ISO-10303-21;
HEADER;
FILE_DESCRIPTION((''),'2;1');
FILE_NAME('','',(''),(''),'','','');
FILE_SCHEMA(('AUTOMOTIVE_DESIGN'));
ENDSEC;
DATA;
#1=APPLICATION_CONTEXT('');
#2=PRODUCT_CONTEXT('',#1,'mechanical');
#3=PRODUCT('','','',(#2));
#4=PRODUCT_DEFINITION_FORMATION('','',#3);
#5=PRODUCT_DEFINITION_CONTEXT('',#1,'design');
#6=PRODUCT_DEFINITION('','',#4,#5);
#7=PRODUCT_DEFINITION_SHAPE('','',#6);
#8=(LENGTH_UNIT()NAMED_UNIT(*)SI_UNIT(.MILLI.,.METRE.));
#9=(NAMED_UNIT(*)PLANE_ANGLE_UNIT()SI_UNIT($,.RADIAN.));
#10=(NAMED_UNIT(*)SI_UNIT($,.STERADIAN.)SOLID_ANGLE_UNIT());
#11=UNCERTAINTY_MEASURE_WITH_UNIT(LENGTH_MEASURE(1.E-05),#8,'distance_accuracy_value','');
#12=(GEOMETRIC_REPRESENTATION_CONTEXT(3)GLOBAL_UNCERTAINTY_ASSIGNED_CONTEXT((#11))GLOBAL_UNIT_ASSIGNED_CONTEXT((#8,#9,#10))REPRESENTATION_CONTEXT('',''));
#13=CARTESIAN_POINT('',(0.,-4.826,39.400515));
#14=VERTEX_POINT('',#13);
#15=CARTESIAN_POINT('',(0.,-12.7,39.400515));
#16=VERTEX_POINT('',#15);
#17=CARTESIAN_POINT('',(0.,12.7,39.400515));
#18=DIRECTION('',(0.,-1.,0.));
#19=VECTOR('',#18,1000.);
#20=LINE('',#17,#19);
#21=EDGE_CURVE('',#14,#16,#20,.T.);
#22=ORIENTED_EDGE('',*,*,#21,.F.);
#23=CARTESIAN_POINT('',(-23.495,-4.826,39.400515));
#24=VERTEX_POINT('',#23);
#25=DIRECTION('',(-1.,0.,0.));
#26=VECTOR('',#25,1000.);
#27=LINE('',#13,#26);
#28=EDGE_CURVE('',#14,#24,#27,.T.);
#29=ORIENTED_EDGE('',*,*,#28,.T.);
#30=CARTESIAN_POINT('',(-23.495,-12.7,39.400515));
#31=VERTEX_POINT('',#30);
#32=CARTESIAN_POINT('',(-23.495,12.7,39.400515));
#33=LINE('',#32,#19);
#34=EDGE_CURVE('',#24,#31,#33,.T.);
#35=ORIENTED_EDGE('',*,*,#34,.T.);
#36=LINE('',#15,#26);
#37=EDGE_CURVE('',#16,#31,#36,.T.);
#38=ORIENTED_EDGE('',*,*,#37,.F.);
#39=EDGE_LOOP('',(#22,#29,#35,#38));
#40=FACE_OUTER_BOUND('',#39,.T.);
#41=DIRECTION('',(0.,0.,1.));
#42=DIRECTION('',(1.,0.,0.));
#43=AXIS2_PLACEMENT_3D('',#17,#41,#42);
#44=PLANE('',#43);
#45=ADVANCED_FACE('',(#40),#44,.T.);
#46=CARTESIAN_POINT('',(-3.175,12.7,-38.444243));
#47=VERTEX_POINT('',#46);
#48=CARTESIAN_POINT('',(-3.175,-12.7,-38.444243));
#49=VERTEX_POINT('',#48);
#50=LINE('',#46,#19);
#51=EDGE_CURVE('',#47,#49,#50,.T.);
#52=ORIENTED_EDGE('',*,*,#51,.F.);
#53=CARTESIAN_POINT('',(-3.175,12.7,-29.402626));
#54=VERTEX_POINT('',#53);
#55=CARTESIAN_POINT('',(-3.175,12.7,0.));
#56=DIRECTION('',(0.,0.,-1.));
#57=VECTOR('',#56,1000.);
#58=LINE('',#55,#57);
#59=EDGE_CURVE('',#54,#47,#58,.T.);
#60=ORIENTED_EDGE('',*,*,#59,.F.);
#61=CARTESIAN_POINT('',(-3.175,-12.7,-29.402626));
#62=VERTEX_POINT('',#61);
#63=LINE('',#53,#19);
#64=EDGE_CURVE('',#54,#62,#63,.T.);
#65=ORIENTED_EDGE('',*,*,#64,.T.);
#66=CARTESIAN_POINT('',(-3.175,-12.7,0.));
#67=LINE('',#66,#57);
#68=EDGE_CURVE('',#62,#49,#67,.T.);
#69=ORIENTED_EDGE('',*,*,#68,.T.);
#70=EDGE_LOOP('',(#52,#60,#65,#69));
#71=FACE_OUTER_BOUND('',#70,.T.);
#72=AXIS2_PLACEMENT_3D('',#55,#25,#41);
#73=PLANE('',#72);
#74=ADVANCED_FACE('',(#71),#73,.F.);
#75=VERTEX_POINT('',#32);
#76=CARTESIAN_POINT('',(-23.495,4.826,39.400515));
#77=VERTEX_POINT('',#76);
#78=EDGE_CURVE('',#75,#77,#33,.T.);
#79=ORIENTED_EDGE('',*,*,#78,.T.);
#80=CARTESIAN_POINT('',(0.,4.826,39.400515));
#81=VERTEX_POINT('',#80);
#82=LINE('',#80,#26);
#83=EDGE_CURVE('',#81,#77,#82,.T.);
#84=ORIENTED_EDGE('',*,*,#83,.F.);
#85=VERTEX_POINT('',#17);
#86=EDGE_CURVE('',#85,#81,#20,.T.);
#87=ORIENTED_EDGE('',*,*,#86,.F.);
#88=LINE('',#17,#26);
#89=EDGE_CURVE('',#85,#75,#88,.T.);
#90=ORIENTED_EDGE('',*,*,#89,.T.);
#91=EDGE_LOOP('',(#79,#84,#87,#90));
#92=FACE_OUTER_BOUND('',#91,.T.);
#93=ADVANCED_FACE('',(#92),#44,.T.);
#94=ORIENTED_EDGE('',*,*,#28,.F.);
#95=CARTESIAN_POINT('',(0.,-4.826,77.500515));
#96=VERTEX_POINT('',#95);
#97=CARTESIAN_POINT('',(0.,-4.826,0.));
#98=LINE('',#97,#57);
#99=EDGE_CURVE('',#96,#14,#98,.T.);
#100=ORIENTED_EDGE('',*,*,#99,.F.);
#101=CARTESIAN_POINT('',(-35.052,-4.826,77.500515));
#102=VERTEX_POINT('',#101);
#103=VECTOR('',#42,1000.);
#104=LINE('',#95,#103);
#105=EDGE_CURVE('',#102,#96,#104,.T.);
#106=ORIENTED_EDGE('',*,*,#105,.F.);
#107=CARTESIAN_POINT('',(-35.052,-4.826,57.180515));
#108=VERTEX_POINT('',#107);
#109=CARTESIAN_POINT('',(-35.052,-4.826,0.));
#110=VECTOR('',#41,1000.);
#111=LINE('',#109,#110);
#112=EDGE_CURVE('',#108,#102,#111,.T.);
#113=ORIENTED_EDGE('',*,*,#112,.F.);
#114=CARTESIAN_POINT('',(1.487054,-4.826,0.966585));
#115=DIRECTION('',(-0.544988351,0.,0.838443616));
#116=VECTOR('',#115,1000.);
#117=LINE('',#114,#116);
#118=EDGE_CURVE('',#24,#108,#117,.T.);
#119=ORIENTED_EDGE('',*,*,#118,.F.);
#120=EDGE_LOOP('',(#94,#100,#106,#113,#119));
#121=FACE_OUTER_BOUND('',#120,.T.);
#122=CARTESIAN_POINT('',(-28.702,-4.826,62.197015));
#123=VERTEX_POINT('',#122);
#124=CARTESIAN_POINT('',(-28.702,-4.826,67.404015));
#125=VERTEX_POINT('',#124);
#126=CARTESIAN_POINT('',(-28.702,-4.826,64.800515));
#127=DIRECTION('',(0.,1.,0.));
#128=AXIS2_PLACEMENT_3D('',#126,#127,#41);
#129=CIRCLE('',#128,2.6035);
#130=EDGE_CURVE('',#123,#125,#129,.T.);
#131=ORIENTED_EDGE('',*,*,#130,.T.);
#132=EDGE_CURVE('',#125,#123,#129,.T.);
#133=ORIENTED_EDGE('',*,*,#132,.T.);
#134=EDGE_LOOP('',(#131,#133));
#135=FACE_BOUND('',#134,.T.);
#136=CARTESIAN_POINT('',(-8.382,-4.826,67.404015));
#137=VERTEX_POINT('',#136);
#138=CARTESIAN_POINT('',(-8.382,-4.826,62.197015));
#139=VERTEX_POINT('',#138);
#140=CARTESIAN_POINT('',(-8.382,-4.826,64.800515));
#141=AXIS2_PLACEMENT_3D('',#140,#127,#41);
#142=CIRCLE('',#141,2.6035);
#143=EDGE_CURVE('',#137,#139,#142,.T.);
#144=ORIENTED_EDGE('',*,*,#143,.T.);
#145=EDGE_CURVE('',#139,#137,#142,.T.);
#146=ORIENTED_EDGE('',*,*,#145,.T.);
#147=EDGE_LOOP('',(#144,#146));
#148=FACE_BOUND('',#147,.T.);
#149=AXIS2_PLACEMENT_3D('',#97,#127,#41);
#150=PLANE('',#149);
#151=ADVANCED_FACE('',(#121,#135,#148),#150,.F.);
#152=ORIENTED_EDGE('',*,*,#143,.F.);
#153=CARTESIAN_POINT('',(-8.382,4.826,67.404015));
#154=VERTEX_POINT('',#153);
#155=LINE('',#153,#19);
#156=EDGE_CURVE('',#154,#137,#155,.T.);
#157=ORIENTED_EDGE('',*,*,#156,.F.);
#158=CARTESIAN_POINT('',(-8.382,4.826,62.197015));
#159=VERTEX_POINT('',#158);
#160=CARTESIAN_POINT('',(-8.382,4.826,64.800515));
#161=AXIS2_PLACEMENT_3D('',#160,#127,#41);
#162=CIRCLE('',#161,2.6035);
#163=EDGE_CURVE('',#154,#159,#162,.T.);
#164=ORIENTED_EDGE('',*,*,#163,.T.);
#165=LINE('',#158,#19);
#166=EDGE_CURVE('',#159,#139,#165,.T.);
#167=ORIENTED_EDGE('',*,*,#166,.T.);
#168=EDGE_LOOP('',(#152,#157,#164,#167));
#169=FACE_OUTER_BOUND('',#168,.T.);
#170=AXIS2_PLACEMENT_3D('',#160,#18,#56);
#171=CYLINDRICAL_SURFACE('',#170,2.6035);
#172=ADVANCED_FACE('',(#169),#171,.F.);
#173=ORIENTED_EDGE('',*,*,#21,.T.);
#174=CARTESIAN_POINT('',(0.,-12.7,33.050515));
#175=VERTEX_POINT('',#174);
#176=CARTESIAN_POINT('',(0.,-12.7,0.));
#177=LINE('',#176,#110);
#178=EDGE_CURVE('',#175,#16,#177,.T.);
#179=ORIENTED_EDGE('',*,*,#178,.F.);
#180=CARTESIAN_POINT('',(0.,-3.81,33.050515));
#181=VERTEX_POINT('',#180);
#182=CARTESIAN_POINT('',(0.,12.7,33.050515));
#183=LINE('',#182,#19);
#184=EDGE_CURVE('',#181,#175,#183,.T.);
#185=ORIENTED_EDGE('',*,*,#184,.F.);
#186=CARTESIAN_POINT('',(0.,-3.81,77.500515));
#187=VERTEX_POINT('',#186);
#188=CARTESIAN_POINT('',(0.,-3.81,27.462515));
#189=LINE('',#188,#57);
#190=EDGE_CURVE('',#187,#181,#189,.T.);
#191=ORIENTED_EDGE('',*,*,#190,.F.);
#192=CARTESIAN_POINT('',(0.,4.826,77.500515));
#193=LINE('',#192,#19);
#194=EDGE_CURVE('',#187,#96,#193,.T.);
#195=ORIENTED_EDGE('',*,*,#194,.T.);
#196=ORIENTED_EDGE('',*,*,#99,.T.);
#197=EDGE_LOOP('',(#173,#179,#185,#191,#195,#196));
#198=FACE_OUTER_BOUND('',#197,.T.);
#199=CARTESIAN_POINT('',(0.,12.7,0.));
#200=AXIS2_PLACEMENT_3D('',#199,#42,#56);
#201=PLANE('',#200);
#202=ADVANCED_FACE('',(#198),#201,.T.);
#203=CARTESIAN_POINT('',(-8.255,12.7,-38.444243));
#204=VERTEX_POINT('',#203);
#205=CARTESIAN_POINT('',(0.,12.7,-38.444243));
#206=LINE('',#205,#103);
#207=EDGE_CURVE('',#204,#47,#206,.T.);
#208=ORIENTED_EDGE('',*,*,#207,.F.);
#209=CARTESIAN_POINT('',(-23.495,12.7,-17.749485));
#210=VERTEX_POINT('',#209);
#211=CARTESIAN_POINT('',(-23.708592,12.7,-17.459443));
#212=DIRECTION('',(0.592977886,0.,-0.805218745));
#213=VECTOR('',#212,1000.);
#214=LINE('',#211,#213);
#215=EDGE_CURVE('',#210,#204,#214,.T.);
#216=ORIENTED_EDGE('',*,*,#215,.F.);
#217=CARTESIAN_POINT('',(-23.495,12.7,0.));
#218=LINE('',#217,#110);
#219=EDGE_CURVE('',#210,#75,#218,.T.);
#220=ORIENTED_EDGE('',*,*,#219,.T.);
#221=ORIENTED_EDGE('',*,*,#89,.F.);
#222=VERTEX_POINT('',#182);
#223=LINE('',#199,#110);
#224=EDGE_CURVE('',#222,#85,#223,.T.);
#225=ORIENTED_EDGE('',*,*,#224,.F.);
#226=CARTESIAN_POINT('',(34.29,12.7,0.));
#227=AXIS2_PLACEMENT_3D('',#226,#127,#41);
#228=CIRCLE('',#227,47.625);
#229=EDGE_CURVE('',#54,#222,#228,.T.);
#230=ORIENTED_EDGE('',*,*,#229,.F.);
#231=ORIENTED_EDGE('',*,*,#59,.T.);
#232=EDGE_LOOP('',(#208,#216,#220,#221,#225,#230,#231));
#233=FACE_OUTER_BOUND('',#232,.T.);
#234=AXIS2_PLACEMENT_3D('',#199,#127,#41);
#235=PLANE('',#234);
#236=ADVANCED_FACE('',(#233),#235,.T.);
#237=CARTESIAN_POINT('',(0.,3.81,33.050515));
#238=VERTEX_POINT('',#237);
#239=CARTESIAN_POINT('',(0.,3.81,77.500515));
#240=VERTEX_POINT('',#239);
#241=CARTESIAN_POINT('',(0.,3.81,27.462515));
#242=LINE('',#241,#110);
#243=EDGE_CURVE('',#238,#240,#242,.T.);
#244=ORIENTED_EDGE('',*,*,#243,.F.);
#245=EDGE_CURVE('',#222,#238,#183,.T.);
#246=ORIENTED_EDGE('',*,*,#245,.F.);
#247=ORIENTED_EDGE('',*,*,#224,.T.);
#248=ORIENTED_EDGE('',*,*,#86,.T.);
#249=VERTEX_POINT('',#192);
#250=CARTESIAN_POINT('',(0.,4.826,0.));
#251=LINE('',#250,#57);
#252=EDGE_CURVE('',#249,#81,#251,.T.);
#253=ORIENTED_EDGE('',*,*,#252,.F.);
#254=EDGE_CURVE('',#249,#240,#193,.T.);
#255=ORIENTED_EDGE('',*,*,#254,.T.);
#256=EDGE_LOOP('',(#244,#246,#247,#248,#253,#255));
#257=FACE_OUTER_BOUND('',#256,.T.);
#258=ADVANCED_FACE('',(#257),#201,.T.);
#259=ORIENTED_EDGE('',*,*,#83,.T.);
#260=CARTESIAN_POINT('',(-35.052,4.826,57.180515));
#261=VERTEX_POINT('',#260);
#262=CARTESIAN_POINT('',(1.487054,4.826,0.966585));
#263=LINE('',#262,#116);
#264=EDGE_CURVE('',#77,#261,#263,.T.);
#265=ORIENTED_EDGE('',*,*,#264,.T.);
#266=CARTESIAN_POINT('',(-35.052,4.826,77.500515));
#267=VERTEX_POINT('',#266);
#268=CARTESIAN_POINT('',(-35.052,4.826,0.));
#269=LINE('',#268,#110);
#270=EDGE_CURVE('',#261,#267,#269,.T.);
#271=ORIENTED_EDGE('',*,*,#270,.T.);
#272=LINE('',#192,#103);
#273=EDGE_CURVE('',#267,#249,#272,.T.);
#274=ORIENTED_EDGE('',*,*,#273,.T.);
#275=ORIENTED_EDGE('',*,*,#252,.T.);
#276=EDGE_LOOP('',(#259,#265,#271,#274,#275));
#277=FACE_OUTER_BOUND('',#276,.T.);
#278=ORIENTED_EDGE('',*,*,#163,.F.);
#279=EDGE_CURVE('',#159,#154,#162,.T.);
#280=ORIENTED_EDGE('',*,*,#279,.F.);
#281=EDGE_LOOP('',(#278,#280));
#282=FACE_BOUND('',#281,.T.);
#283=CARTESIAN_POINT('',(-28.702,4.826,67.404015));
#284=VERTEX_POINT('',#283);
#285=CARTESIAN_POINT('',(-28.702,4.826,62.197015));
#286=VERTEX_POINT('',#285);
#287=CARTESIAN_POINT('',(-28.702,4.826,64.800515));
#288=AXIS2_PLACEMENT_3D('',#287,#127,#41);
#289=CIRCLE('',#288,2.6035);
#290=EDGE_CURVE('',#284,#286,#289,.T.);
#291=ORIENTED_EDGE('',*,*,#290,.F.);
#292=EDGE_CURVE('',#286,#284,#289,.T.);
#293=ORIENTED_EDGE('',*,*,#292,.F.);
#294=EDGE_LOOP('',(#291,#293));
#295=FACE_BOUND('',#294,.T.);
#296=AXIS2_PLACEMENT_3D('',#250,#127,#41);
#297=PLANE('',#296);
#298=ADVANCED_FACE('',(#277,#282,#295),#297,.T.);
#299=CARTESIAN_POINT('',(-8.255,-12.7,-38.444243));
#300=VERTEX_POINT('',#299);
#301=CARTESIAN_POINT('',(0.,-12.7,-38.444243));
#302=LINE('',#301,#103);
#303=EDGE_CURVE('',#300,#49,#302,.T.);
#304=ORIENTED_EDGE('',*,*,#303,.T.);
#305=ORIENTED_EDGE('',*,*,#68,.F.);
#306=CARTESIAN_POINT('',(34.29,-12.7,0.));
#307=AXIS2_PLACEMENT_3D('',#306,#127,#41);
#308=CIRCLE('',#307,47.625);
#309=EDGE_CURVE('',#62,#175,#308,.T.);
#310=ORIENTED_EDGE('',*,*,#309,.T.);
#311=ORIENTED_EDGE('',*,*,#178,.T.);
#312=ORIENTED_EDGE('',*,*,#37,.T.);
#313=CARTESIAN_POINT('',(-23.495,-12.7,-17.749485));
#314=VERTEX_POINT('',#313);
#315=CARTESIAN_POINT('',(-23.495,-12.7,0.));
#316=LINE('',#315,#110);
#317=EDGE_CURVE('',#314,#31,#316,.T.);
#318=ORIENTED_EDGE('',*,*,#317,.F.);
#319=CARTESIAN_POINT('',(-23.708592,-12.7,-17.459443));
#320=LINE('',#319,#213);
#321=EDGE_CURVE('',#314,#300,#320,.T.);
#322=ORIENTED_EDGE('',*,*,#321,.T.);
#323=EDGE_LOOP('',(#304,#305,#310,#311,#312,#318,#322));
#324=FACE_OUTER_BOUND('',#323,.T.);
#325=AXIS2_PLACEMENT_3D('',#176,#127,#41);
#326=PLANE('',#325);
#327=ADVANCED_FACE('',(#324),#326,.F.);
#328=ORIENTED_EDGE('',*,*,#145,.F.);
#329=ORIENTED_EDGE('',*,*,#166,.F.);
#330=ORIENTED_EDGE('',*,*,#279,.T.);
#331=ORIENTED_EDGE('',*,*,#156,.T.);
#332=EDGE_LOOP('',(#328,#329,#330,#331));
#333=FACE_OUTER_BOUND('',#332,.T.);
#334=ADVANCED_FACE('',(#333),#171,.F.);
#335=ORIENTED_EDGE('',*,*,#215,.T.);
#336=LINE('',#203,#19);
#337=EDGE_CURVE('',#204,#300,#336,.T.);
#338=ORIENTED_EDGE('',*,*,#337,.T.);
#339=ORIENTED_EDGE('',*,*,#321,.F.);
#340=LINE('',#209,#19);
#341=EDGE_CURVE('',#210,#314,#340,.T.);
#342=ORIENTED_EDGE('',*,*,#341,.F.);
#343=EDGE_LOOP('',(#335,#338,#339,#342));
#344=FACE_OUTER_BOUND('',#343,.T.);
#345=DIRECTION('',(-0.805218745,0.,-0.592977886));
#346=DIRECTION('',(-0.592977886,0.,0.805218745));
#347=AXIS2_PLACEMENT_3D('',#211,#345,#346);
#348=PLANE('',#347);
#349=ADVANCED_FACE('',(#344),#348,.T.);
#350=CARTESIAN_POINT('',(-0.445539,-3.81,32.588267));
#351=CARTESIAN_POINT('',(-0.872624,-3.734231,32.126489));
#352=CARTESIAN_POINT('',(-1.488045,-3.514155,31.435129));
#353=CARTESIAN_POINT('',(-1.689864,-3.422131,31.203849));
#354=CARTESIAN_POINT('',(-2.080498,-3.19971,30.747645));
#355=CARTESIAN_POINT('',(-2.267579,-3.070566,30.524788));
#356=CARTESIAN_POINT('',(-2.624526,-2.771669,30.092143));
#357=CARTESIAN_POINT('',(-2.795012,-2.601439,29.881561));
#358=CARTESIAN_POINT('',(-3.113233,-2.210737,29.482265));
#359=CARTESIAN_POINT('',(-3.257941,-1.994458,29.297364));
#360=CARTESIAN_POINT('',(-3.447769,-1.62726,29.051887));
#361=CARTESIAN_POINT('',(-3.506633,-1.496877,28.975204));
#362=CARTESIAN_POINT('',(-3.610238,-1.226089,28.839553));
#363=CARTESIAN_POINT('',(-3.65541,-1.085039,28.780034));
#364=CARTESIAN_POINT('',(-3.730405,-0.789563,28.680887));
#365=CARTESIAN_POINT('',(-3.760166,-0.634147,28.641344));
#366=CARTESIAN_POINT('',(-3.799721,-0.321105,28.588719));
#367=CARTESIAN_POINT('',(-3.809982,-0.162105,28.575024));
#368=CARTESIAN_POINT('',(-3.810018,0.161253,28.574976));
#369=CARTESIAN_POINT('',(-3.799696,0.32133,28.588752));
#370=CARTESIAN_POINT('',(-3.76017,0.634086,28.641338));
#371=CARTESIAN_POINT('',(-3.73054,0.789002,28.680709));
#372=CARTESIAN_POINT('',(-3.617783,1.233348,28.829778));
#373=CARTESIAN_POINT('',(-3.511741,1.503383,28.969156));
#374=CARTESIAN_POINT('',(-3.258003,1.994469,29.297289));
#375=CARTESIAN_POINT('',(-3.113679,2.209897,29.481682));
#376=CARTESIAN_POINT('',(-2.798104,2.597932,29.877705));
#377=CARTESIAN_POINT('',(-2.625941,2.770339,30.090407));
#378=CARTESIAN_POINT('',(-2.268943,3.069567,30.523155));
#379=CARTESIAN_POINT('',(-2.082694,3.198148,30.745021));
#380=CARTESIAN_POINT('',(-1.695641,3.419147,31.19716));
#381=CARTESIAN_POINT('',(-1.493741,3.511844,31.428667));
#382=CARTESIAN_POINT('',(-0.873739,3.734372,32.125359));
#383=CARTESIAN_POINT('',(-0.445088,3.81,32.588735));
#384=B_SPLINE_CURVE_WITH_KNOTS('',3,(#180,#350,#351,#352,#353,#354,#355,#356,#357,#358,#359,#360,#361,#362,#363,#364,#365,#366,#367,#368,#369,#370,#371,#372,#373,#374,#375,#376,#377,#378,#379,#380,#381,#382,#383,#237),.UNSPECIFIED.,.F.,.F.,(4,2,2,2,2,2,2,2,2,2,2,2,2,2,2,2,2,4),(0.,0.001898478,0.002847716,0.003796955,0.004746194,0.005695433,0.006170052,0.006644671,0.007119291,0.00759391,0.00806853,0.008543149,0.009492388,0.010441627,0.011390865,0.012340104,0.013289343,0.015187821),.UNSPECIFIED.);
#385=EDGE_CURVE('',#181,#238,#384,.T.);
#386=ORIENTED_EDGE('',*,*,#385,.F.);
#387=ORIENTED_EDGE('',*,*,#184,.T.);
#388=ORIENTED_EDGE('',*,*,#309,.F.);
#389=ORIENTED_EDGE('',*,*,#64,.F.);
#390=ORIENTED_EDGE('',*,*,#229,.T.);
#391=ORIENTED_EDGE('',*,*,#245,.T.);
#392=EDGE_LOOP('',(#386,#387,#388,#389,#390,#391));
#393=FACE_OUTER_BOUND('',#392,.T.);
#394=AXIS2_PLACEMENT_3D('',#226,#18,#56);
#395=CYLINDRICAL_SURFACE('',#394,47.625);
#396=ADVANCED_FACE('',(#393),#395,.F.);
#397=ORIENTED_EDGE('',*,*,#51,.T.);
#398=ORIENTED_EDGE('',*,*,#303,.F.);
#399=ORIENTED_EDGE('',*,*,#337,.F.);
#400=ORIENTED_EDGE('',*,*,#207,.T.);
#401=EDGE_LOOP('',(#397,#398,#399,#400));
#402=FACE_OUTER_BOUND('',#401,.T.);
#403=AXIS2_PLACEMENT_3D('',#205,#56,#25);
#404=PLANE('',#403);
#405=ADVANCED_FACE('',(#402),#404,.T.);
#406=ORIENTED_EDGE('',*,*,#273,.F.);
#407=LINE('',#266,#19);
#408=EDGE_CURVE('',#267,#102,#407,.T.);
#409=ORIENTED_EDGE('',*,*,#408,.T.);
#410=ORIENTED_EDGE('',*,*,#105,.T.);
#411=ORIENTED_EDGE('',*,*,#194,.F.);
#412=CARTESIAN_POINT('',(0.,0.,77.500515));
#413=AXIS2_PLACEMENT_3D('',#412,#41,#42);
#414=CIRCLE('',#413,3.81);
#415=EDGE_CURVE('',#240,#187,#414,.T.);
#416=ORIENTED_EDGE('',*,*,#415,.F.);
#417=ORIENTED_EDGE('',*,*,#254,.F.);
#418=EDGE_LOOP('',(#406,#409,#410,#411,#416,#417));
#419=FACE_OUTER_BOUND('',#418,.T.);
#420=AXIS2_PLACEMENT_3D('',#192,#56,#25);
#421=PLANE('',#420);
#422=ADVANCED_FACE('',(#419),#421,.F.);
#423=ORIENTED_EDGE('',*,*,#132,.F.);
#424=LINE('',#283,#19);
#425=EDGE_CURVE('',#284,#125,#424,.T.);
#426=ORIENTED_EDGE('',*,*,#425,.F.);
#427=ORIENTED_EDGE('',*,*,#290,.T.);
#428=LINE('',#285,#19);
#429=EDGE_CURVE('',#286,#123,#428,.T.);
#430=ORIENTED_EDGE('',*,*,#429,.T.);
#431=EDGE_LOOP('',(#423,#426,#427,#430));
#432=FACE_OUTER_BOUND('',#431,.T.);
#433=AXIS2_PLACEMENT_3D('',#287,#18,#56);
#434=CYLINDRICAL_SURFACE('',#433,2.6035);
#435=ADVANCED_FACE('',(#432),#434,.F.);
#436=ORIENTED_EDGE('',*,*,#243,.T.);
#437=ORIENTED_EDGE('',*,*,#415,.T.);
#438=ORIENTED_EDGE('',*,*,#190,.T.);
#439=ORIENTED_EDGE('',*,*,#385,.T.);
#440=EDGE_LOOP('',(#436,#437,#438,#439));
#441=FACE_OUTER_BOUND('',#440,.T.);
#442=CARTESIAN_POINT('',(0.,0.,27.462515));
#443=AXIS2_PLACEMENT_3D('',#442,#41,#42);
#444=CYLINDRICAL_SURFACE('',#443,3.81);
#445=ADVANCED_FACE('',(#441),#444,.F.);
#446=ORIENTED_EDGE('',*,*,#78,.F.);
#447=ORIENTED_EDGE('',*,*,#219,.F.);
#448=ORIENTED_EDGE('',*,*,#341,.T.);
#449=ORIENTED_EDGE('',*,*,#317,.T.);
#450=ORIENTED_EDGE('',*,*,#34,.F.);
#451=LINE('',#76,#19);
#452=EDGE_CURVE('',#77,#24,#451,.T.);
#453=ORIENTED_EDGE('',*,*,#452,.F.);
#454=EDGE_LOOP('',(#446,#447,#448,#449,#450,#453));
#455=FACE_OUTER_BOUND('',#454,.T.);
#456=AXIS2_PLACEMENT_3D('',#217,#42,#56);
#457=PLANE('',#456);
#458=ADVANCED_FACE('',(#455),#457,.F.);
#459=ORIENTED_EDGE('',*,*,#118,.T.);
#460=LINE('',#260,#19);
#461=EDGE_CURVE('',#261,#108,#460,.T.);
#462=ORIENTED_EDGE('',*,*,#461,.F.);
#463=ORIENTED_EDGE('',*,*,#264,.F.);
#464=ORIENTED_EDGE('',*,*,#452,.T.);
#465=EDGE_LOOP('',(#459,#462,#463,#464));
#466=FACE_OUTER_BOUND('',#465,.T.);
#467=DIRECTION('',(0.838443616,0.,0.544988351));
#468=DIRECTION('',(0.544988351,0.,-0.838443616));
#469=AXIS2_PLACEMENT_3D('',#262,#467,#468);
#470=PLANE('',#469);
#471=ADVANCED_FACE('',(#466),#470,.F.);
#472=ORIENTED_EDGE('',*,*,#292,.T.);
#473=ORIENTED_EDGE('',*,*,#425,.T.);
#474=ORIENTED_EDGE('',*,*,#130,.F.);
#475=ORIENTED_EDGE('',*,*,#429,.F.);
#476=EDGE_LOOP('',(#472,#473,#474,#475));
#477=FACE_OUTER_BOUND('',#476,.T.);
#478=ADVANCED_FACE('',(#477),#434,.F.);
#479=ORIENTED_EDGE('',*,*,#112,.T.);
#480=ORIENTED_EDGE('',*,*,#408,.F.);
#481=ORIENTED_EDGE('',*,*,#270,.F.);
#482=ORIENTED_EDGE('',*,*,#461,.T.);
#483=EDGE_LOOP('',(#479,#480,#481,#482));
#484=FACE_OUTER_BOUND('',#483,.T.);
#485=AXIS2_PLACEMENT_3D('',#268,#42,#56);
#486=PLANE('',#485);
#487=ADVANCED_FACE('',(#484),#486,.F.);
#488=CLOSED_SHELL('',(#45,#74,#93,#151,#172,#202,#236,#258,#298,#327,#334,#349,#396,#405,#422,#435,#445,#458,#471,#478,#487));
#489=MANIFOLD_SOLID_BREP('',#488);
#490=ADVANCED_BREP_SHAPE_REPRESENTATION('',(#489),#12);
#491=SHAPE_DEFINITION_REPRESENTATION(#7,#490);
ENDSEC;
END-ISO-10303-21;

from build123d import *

# Parameters (mm, degrees)
BOSS_EXTRUDE1_DEPTH = 12.7
SKETCH1_5_R         = 2.6035
BOSS_EXTRUDE2_DEPTH = 4.826
SKETCH2_R           = 3.81
CUT_EXTRUDE1_DEPTH  = 50.038


with BuildPart() as part:
    # Sketch1 → Boss-Extrude1 (new, symmetric)
    with BuildSketch(Plane(origin=(0, 0, 0), x_dir=(1, 0, 0), z_dir=(0, 1, 0))):
        with BuildLine():
            Line((-23.495, 17.749485254), (-23.495, -39.400514746))
            Line((-23.495, -39.400514746), (0, -39.400514746))
            Line((0, -39.400514746), (0, -33.050514746))
            ThreePointArc((0, -33.050514746), (-13.273575299, -2.418042558), (-3.175, 29.402625733))
            Line((-3.175, 29.402625733), (-3.175, 38.444242963))
            Line((-3.175, 38.444242963), (-8.255, 38.444242963))
            Line((-8.255, 38.444242963), (-23.495, 17.749485254))
        make_face()
    extrude(amount=BOSS_EXTRUDE1_DEPTH, both=True)

    # Sketch1<5> → Boss-Extrude2 (add, symmetric)
    with BuildSketch(Plane(origin=(0, 0, 0), x_dir=(1, 0, 0), z_dir=(0, 1, 0))):
        Polygon((0, -39.400514746), (-23.495, -39.400514746), (-35.052, -57.180514746), (-35.052, -77.500514746), (0, -77.500514746), align=None)
        with Locations(Location((-28.702, -64.800514746, 0), (0, 0, 270))):
            Circle(SKETCH1_5_R, mode=Mode.SUBTRACT)
        with Locations(Location((-8.382, -64.800514746, 0), (0, 0, 270))):
            Circle(SKETCH1_5_R, mode=Mode.SUBTRACT)
    extrude(amount=BOSS_EXTRUDE2_DEPTH, both=True)

    # Sketch2 → Cut-Extrude1 (cut)
    with BuildSketch(Plane.XY.offset(77.500514746)):
        Circle(SKETCH2_R)
    extrude(amount=-CUT_EXTRUDE1_DEPTH, mode=Mode.SUBTRACT)


solid = part.part
